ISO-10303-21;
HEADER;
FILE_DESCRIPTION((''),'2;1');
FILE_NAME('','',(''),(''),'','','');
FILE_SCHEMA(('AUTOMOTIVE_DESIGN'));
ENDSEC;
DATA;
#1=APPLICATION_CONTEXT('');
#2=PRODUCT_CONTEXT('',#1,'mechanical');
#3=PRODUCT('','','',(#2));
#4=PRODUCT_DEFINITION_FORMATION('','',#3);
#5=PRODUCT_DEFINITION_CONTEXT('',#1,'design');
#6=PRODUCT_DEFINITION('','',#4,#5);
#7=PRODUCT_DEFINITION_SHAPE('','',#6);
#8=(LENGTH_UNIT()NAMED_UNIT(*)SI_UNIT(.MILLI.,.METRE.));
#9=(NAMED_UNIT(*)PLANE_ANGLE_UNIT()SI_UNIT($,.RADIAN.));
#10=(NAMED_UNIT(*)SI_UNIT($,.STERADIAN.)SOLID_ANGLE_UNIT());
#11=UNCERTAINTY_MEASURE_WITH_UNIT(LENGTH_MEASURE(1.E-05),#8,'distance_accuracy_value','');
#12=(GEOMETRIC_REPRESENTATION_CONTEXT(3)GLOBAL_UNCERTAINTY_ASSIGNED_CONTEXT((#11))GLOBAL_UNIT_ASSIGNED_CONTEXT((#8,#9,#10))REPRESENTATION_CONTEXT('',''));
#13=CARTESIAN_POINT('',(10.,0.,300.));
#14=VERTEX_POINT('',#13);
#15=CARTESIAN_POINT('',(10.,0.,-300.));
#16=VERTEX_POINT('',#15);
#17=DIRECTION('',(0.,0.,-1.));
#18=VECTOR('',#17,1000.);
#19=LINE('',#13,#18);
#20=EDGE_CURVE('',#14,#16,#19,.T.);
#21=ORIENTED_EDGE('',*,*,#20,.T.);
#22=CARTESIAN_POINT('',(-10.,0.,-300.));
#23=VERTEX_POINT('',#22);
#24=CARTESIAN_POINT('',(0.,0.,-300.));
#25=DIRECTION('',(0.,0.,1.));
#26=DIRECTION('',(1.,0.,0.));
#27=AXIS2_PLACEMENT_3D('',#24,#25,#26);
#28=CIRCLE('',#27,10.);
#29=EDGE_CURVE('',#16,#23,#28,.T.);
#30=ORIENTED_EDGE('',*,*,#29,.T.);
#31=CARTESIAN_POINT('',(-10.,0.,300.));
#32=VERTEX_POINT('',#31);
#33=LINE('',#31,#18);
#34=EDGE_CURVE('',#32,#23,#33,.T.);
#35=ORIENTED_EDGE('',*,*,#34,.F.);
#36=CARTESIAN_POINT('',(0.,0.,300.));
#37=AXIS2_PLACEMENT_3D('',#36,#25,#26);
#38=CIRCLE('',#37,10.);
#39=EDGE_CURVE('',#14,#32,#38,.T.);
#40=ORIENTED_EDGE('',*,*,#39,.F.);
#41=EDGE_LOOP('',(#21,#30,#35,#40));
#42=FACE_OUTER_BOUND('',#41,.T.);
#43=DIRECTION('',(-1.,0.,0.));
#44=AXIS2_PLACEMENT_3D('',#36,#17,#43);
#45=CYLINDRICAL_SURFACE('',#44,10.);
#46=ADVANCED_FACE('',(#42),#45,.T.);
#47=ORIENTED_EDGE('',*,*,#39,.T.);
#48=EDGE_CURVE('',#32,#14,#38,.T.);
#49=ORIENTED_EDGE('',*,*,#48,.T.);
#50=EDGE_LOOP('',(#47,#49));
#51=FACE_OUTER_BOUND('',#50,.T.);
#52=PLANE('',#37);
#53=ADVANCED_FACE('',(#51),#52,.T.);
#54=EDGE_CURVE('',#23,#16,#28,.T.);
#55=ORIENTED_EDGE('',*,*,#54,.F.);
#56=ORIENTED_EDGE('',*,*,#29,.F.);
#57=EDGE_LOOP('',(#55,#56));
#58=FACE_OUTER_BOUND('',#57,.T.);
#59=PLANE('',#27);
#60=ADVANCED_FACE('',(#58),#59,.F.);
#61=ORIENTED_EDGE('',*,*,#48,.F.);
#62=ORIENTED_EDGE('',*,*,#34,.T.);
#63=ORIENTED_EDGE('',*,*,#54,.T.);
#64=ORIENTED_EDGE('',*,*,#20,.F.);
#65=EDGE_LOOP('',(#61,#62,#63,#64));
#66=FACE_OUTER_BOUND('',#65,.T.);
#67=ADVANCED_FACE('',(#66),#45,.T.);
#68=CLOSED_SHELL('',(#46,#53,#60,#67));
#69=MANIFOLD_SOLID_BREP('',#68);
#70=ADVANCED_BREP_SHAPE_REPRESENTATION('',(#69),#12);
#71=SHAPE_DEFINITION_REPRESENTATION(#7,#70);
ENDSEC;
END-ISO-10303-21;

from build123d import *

# Parameters (mm, degrees)
SKETCH_1_R      = 10
EXTRUDE_1_DEPTH = 300


with BuildPart() as part:
    # 草图1 → 凸台-拉伸1 (new, symmetric)
    with BuildSketch(Plane.XY):
        Circle(SKETCH_1_R)
    extrude(amount=EXTRUDE_1_DEPTH, both=True)


solid = part.part
